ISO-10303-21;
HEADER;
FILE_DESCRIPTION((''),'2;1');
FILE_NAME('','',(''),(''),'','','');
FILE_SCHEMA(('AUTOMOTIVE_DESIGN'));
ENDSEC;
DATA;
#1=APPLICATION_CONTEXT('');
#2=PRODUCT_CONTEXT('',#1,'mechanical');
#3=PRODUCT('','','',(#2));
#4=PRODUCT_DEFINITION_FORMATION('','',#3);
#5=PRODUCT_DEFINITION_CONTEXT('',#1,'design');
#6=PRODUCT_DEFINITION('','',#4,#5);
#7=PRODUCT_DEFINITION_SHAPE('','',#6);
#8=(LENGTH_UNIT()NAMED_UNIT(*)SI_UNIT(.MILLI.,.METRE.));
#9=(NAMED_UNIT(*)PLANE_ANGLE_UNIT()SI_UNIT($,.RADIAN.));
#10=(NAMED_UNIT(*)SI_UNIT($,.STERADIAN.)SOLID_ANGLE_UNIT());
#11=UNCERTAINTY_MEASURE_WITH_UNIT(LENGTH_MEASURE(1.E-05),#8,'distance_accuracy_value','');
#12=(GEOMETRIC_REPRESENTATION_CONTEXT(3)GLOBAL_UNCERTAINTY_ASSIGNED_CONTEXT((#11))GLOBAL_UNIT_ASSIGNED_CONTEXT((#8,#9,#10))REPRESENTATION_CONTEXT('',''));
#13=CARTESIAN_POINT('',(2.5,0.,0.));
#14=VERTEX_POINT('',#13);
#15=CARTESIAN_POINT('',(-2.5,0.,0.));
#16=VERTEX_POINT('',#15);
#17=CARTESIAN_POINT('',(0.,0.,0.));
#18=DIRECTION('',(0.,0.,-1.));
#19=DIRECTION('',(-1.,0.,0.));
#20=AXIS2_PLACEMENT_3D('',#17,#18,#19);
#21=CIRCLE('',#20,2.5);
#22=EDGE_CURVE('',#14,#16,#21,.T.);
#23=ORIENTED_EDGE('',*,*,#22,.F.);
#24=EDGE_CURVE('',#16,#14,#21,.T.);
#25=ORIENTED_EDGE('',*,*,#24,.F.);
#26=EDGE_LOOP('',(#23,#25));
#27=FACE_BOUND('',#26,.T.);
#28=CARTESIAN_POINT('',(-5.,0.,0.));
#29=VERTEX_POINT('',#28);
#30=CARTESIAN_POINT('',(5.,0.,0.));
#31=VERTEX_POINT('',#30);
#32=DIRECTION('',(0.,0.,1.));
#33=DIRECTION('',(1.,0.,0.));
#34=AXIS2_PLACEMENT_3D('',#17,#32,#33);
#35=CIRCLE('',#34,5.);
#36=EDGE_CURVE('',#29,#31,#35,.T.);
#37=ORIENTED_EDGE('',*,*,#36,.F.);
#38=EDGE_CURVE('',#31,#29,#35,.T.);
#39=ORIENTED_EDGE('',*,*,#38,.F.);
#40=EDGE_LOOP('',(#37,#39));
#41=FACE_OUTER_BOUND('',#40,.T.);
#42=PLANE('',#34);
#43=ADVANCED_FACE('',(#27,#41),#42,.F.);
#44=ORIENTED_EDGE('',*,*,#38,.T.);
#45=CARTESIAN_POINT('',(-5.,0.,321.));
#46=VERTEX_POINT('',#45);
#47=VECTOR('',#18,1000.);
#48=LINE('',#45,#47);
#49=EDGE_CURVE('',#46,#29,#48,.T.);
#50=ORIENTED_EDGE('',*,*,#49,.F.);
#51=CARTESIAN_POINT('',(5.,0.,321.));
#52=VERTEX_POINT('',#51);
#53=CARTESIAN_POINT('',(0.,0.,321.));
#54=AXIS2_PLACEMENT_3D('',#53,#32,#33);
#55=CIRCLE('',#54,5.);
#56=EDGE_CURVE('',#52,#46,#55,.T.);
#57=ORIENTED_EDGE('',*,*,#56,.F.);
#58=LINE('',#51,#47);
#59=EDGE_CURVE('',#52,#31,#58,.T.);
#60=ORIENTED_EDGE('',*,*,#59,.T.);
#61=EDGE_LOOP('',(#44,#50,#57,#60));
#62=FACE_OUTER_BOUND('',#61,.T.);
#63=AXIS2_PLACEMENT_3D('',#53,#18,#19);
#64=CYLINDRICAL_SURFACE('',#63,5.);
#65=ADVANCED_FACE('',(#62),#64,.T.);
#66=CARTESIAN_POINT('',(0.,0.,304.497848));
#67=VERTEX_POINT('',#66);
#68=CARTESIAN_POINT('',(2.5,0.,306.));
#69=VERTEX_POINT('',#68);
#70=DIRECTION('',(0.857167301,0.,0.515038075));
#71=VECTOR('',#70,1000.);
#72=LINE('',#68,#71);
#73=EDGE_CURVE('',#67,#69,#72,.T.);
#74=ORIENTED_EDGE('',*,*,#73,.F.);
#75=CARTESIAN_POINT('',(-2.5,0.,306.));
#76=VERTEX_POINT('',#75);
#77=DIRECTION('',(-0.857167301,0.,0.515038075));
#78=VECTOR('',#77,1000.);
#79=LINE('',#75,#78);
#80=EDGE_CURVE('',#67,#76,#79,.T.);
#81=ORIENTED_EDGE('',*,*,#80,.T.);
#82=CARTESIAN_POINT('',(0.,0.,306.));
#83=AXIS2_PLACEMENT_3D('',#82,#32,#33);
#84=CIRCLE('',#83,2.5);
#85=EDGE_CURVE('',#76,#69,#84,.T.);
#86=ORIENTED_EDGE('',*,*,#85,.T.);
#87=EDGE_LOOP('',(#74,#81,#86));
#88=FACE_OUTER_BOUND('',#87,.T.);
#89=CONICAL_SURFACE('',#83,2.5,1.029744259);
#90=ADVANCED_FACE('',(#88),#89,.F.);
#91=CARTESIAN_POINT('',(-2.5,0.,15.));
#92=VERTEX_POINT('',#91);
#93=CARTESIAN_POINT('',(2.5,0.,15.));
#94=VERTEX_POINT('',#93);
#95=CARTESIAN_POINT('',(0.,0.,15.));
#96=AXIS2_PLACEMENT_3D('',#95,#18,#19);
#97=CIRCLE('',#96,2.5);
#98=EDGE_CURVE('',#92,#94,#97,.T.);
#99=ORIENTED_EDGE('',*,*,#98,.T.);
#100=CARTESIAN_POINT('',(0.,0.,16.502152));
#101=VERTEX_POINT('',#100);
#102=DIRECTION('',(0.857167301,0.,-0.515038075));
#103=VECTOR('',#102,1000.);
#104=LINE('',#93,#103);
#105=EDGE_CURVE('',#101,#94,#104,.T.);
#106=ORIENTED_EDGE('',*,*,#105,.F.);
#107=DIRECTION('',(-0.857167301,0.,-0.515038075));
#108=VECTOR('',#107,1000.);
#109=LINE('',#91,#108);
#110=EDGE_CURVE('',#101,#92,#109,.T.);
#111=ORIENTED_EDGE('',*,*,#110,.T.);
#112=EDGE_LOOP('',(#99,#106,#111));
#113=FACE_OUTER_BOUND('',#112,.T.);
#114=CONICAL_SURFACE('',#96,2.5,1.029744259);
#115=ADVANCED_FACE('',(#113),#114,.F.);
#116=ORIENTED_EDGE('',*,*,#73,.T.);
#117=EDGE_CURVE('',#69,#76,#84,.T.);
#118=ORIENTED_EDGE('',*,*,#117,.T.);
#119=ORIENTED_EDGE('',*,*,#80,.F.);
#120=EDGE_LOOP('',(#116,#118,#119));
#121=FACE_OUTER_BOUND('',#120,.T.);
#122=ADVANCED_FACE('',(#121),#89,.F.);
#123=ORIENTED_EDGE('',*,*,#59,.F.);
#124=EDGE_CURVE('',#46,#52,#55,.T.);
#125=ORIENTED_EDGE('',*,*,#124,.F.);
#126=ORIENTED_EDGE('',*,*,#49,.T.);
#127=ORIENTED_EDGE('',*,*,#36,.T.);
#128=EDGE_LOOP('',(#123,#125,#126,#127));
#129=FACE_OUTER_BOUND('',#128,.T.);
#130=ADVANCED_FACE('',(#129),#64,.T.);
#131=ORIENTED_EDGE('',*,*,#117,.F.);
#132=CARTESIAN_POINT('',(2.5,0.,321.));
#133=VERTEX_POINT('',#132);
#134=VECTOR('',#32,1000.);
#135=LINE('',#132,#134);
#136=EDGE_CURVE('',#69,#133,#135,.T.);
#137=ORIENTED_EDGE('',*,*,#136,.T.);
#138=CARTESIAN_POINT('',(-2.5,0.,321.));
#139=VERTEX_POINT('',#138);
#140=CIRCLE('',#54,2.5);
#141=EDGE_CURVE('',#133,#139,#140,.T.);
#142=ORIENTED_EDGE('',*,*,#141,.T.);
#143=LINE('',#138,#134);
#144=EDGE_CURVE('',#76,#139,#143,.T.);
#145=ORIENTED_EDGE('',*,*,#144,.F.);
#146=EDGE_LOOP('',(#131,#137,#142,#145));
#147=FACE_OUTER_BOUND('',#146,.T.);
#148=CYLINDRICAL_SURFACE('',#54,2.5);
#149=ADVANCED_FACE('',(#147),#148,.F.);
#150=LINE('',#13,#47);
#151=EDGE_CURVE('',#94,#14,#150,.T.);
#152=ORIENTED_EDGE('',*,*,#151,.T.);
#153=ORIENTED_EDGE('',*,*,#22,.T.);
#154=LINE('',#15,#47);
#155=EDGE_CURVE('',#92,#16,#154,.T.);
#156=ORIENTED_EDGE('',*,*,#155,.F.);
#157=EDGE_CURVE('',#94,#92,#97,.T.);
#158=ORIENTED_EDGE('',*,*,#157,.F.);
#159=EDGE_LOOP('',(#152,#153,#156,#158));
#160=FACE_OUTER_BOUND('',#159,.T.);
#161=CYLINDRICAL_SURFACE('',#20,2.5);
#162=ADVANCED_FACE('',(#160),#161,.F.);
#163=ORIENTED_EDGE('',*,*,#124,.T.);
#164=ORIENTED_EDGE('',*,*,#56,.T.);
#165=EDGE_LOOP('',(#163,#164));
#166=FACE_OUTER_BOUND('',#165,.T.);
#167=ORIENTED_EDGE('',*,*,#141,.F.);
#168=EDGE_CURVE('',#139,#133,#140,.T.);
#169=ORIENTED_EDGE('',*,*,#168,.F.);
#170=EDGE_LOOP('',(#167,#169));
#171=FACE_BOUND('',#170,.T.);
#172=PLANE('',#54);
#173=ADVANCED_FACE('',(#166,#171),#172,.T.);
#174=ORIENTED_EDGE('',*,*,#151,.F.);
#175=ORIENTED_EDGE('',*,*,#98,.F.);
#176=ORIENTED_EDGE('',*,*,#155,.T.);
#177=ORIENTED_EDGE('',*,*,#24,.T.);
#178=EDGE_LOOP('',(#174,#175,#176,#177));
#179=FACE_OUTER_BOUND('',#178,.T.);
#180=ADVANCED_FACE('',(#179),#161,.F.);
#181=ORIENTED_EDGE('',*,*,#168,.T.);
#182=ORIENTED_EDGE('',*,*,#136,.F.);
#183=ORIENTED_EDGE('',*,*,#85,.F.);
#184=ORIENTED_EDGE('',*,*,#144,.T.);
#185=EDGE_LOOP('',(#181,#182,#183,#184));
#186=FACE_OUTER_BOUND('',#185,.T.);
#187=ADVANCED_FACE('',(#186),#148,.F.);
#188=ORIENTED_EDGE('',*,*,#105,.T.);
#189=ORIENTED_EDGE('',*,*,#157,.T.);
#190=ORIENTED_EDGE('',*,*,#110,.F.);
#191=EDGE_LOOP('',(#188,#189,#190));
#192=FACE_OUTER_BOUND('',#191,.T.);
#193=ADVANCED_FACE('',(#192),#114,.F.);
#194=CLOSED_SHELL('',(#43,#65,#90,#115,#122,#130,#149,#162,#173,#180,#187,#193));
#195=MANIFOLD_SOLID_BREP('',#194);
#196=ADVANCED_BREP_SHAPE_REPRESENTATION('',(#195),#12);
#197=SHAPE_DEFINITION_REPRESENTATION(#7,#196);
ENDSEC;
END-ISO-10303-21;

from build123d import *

# Parameters (mm, degrees)
SKETCH1_R             = 5
BOSS_EXTRUDE1_DEPTH   = 321
M6_TAPPED_HOLE1_D     = 5
M6_TAPPED_HOLE1_DEPTH = 15
M6_TAPPED_HOLE1_TIP   = 1.502151548
M6_TAPPED_HOLE2_D     = 5
M6_TAPPED_HOLE2_DEPTH = 15
M6_TAPPED_HOLE2_TIP   = 1.502151548


with BuildPart() as part:
    # Sketch1 → Boss-Extrude1 (new body)
    with BuildSketch(Plane.XY):
        Circle(SKETCH1_R)
    extrude(amount=BOSS_EXTRUDE1_DEPTH)

    # M6 Tapped Hole1
    with Locations(Plane.XY.offset(321)):
        with Locations((0, 0)):
            Hole(M6_TAPPED_HOLE1_D / 2, depth=M6_TAPPED_HOLE1_DEPTH)
            with Locations((0, 0, -(M6_TAPPED_HOLE1_DEPTH + M6_TAPPED_HOLE1_TIP / 2))):  # 118° drill point
                Cone(0, M6_TAPPED_HOLE1_D / 2, M6_TAPPED_HOLE1_TIP, mode=Mode.SUBTRACT)

    # M6 Tapped Hole2
    with Locations(Plane(origin=(0, 0, 0), x_dir=(-1, 0, 0), z_dir=(0, 0, -1))):
        with Locations((0, 0)):
            Hole(M6_TAPPED_HOLE2_D / 2, depth=M6_TAPPED_HOLE2_DEPTH)
            with Locations((0, 0, -(M6_TAPPED_HOLE2_DEPTH + M6_TAPPED_HOLE2_TIP / 2))):  # 118° drill point
                Cone(0, M6_TAPPED_HOLE2_D / 2, M6_TAPPED_HOLE2_TIP, mode=Mode.SUBTRACT)


solid = part.part
